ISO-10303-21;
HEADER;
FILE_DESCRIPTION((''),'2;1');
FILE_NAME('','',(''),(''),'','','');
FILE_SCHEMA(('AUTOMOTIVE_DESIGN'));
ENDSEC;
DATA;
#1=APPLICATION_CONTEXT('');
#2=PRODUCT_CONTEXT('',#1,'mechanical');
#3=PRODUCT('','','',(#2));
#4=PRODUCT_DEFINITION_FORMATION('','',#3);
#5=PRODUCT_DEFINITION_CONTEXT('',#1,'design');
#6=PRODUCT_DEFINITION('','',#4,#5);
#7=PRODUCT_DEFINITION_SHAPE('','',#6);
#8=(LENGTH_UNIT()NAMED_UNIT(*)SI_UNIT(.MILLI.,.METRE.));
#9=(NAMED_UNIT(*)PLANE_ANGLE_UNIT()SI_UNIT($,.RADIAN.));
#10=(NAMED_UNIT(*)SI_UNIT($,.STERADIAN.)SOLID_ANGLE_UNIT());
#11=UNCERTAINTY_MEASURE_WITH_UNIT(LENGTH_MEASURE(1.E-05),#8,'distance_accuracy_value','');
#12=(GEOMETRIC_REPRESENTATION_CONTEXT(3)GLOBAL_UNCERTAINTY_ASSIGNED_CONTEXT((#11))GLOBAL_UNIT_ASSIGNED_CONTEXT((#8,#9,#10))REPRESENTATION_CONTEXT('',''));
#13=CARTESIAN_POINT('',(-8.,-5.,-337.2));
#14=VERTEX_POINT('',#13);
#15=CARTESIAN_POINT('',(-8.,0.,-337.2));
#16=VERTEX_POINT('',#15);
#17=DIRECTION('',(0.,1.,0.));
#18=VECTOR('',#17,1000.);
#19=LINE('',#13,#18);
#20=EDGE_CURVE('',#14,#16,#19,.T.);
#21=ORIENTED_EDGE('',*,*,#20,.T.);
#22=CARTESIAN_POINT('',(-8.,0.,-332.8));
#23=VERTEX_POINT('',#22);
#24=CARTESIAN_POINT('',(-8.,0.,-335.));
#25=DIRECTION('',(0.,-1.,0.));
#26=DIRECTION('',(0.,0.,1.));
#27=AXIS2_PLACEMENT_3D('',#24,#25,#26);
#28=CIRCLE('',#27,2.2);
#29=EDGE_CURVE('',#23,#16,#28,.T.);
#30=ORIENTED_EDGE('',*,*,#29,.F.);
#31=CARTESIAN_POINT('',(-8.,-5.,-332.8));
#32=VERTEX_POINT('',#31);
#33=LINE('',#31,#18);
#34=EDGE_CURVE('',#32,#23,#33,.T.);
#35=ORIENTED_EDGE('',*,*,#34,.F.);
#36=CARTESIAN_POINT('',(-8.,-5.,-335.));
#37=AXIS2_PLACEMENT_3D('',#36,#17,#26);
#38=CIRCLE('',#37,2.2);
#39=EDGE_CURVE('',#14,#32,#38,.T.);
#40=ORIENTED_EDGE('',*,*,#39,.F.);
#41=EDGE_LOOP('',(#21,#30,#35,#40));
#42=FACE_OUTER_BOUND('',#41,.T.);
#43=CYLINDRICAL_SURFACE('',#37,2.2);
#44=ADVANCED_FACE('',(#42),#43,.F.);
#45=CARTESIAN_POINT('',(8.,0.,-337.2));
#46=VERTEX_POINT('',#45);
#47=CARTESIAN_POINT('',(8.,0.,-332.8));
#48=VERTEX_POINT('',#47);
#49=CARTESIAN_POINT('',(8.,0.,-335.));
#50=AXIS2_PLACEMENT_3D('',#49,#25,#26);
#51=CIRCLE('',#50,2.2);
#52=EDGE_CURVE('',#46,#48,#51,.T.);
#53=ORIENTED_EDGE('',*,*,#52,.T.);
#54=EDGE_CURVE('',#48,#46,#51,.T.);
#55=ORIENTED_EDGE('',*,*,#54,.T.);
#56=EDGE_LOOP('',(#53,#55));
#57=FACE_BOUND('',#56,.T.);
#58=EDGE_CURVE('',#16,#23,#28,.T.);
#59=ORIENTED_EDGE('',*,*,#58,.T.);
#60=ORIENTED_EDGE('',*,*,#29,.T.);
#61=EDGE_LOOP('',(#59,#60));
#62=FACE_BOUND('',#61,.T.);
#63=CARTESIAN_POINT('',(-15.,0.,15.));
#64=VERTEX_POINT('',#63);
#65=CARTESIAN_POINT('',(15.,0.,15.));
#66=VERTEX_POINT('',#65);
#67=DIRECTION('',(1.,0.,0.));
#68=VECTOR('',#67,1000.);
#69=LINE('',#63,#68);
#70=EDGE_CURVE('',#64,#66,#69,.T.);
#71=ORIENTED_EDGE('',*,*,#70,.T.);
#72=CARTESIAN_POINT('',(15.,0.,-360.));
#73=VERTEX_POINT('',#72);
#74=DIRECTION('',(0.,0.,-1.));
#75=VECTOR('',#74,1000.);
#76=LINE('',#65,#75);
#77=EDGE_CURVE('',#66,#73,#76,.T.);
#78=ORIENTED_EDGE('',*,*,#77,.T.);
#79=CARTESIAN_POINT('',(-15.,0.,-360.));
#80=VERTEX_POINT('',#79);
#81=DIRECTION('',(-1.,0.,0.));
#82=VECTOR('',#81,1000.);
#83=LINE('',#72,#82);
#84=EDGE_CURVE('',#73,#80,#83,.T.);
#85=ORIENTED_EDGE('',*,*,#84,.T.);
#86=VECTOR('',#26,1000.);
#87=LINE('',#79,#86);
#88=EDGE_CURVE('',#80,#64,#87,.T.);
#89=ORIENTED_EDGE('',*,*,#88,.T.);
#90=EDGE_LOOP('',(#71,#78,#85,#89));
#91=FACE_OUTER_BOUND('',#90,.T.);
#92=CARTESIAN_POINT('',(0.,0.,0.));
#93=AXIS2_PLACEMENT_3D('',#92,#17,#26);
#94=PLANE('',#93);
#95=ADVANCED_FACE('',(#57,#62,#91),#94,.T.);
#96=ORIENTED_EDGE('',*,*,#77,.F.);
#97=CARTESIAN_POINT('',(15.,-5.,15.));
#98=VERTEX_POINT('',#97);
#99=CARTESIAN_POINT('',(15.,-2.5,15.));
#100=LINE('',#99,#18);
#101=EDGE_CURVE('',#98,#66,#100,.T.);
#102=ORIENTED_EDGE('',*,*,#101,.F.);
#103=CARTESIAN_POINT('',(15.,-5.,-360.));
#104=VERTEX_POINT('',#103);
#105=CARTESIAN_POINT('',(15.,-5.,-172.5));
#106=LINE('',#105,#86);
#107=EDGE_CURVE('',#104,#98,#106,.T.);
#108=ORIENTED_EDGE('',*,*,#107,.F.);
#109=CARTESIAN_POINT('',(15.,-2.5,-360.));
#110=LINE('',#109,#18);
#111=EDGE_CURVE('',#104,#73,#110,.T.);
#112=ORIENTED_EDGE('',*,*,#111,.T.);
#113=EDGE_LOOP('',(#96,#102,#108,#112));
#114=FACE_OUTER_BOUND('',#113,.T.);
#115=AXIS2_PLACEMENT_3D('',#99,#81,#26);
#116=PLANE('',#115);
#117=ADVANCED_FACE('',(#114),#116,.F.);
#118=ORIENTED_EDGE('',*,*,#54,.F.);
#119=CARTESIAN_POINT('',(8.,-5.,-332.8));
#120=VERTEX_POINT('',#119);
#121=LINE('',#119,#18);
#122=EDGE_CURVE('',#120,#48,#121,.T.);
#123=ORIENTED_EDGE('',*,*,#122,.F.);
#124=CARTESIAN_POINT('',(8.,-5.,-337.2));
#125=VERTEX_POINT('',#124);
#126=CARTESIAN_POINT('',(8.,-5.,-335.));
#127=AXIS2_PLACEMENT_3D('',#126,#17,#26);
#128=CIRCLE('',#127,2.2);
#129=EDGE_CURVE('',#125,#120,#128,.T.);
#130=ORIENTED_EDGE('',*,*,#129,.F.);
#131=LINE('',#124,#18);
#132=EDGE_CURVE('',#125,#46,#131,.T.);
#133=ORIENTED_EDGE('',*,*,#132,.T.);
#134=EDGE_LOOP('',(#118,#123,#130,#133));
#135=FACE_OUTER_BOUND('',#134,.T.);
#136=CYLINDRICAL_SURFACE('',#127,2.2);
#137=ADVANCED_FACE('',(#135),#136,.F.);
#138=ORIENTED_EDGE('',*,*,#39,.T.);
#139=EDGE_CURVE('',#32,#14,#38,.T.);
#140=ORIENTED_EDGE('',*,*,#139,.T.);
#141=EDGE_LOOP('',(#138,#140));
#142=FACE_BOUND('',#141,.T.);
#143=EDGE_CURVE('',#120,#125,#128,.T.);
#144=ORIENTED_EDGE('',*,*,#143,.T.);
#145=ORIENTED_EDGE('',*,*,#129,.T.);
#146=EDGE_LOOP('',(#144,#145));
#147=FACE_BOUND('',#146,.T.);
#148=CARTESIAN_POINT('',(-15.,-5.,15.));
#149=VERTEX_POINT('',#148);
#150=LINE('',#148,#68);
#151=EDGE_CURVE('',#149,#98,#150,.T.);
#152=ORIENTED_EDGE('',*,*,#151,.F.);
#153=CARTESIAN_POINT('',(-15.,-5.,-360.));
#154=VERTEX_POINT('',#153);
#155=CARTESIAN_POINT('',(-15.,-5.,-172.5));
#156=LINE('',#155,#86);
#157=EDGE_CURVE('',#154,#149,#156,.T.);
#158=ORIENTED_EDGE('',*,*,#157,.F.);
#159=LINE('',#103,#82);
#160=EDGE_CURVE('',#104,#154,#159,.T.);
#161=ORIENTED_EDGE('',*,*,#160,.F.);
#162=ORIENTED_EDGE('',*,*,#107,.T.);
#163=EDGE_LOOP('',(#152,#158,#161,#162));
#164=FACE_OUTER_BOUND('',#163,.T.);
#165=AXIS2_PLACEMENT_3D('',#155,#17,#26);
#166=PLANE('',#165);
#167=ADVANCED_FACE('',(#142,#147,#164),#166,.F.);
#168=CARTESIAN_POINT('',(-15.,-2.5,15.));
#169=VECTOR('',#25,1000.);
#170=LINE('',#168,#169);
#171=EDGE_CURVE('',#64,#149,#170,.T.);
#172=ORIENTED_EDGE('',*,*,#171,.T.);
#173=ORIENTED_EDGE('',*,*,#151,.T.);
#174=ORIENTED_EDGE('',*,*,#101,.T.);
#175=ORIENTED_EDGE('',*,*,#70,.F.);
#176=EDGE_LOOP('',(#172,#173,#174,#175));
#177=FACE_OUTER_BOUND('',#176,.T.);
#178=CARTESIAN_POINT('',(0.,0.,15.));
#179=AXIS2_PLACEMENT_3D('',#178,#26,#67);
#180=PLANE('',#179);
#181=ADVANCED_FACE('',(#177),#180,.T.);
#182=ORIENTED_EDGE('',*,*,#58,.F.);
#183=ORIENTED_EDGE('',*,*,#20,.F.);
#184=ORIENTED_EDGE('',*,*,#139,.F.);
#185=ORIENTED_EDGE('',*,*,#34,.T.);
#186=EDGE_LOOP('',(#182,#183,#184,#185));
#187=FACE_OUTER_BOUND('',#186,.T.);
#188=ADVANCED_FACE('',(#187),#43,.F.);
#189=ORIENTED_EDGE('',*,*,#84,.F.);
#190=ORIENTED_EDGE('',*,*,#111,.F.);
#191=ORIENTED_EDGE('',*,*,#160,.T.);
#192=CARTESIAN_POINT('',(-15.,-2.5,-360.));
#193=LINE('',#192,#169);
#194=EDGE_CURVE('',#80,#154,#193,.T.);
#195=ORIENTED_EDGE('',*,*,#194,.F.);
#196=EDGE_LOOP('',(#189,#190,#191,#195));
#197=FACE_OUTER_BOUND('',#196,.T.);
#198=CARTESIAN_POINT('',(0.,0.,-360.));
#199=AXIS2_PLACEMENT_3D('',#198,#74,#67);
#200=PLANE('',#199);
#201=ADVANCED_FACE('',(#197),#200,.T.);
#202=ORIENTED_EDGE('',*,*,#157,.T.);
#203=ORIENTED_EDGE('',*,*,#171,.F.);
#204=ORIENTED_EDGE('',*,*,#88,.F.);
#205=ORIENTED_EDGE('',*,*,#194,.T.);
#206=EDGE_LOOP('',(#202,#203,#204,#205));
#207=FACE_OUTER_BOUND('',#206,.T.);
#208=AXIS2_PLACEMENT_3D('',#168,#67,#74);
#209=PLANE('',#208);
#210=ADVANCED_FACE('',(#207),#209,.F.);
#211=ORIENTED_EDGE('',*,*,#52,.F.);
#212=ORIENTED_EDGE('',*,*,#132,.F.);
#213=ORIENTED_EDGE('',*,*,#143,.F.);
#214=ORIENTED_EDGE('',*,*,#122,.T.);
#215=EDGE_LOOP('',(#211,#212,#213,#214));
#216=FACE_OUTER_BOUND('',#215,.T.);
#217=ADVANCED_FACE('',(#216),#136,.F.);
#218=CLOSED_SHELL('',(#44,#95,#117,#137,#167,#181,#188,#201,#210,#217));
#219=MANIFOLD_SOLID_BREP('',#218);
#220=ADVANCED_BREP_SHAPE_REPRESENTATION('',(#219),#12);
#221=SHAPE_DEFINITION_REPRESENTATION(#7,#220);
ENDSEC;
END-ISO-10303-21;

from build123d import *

# Parameters (mm, degrees)
SKETCH_1_W          = 30
SKETCH_1_H          = 5
EXTRUDE_1_DEPTH     = 15
SKETCH_2_W          = 30
SKETCH_2_H          = 10
EXTRUDE_2_DEPTH     = 172.5
SKETCH_3_R          = 2.2
CUT_EXTRUDE_1_DEPTH = 10
SKETCH_4_W          = 30
SKETCH_4_H          = 2.5
EXTRUDE_3_DEPTH     = 15
SKETCH_5_W          = 30
SKETCH_5_H          = 2.5
EXTRUDE_4_DEPTH     = 15
SKETCH_6_W          = 30
SKETCH_6_H          = 375
CUT_EXTRUDE_2_DEPTH = 5


with BuildPart() as part:
    # 草图1 → 凸台-拉伸1 (new body)
    with BuildSketch(Plane.XY):
        Rectangle(SKETCH_1_W, SKETCH_1_H)
    extrude(amount=EXTRUDE_1_DEPTH)

    # 草图2 → 凸台-拉伸2 (add)
    with BuildSketch(Plane(origin=(0, 0, 0), x_dir=(-1, 0, 0), z_dir=(0, 0, -1))):
        Rectangle(SKETCH_2_W, SKETCH_2_H)
    extrude(amount=EXTRUDE_2_DEPTH)

    # 镜向2: part across plane


with BuildPart() as part_1:
    add(part.part)
    add(part.part.mirror(Plane(origin=(0, 0, -172.5), x_dir=(1, 0, 0), z_dir=(0, 0, -1))))

    # 草图3 → 切除-拉伸1 (cut)
    with BuildSketch(Plane(origin=(0, 5, 0), x_dir=(1, 0, 0), z_dir=(0, 1, 0))):
        with Locations(Location((8, 335, 0), (0, 0, 270))):
            Circle(SKETCH_3_R)
        with Locations(Location((-8, 335, 0), (0, 0, 270))):
            Circle(SKETCH_3_R)
    extrude(amount=-CUT_EXTRUDE_1_DEPTH, mode=Mode.SUBTRACT)

    # 草图4 → 凸台-拉伸3 (add)
    with BuildSketch(Plane(origin=(0, 0, -345), x_dir=(-1, 0, 0), z_dir=(0, 0, -1))):
        with Locations((0, 3.75)):
            Rectangle(SKETCH_4_W, SKETCH_4_H)
        with Locations((0, -3.75)):
            Rectangle(SKETCH_4_W, SKETCH_4_H)
    extrude(amount=EXTRUDE_3_DEPTH)

    # 草图5 → 凸台-拉伸4 (add)
    with BuildSketch(Plane.XY):
        with Locations((0, 3.75)):
            Rectangle(SKETCH_5_W, SKETCH_5_H)
        with Locations((0, -3.75)):
            Rectangle(SKETCH_5_W, SKETCH_5_H)
    extrude(amount=EXTRUDE_4_DEPTH)

    # 草图6 → 切除-拉伸2 (cut)
    with BuildSketch(Plane(origin=(0, 5, 0), x_dir=(1, 0, 0), z_dir=(0, 1, 0))):
        with Locations((0, 172.5)):
            Rectangle(SKETCH_6_W, SKETCH_6_H)
    extrude(amount=-CUT_EXTRUDE_2_DEPTH, mode=Mode.SUBTRACT)


solid = part_1.part
